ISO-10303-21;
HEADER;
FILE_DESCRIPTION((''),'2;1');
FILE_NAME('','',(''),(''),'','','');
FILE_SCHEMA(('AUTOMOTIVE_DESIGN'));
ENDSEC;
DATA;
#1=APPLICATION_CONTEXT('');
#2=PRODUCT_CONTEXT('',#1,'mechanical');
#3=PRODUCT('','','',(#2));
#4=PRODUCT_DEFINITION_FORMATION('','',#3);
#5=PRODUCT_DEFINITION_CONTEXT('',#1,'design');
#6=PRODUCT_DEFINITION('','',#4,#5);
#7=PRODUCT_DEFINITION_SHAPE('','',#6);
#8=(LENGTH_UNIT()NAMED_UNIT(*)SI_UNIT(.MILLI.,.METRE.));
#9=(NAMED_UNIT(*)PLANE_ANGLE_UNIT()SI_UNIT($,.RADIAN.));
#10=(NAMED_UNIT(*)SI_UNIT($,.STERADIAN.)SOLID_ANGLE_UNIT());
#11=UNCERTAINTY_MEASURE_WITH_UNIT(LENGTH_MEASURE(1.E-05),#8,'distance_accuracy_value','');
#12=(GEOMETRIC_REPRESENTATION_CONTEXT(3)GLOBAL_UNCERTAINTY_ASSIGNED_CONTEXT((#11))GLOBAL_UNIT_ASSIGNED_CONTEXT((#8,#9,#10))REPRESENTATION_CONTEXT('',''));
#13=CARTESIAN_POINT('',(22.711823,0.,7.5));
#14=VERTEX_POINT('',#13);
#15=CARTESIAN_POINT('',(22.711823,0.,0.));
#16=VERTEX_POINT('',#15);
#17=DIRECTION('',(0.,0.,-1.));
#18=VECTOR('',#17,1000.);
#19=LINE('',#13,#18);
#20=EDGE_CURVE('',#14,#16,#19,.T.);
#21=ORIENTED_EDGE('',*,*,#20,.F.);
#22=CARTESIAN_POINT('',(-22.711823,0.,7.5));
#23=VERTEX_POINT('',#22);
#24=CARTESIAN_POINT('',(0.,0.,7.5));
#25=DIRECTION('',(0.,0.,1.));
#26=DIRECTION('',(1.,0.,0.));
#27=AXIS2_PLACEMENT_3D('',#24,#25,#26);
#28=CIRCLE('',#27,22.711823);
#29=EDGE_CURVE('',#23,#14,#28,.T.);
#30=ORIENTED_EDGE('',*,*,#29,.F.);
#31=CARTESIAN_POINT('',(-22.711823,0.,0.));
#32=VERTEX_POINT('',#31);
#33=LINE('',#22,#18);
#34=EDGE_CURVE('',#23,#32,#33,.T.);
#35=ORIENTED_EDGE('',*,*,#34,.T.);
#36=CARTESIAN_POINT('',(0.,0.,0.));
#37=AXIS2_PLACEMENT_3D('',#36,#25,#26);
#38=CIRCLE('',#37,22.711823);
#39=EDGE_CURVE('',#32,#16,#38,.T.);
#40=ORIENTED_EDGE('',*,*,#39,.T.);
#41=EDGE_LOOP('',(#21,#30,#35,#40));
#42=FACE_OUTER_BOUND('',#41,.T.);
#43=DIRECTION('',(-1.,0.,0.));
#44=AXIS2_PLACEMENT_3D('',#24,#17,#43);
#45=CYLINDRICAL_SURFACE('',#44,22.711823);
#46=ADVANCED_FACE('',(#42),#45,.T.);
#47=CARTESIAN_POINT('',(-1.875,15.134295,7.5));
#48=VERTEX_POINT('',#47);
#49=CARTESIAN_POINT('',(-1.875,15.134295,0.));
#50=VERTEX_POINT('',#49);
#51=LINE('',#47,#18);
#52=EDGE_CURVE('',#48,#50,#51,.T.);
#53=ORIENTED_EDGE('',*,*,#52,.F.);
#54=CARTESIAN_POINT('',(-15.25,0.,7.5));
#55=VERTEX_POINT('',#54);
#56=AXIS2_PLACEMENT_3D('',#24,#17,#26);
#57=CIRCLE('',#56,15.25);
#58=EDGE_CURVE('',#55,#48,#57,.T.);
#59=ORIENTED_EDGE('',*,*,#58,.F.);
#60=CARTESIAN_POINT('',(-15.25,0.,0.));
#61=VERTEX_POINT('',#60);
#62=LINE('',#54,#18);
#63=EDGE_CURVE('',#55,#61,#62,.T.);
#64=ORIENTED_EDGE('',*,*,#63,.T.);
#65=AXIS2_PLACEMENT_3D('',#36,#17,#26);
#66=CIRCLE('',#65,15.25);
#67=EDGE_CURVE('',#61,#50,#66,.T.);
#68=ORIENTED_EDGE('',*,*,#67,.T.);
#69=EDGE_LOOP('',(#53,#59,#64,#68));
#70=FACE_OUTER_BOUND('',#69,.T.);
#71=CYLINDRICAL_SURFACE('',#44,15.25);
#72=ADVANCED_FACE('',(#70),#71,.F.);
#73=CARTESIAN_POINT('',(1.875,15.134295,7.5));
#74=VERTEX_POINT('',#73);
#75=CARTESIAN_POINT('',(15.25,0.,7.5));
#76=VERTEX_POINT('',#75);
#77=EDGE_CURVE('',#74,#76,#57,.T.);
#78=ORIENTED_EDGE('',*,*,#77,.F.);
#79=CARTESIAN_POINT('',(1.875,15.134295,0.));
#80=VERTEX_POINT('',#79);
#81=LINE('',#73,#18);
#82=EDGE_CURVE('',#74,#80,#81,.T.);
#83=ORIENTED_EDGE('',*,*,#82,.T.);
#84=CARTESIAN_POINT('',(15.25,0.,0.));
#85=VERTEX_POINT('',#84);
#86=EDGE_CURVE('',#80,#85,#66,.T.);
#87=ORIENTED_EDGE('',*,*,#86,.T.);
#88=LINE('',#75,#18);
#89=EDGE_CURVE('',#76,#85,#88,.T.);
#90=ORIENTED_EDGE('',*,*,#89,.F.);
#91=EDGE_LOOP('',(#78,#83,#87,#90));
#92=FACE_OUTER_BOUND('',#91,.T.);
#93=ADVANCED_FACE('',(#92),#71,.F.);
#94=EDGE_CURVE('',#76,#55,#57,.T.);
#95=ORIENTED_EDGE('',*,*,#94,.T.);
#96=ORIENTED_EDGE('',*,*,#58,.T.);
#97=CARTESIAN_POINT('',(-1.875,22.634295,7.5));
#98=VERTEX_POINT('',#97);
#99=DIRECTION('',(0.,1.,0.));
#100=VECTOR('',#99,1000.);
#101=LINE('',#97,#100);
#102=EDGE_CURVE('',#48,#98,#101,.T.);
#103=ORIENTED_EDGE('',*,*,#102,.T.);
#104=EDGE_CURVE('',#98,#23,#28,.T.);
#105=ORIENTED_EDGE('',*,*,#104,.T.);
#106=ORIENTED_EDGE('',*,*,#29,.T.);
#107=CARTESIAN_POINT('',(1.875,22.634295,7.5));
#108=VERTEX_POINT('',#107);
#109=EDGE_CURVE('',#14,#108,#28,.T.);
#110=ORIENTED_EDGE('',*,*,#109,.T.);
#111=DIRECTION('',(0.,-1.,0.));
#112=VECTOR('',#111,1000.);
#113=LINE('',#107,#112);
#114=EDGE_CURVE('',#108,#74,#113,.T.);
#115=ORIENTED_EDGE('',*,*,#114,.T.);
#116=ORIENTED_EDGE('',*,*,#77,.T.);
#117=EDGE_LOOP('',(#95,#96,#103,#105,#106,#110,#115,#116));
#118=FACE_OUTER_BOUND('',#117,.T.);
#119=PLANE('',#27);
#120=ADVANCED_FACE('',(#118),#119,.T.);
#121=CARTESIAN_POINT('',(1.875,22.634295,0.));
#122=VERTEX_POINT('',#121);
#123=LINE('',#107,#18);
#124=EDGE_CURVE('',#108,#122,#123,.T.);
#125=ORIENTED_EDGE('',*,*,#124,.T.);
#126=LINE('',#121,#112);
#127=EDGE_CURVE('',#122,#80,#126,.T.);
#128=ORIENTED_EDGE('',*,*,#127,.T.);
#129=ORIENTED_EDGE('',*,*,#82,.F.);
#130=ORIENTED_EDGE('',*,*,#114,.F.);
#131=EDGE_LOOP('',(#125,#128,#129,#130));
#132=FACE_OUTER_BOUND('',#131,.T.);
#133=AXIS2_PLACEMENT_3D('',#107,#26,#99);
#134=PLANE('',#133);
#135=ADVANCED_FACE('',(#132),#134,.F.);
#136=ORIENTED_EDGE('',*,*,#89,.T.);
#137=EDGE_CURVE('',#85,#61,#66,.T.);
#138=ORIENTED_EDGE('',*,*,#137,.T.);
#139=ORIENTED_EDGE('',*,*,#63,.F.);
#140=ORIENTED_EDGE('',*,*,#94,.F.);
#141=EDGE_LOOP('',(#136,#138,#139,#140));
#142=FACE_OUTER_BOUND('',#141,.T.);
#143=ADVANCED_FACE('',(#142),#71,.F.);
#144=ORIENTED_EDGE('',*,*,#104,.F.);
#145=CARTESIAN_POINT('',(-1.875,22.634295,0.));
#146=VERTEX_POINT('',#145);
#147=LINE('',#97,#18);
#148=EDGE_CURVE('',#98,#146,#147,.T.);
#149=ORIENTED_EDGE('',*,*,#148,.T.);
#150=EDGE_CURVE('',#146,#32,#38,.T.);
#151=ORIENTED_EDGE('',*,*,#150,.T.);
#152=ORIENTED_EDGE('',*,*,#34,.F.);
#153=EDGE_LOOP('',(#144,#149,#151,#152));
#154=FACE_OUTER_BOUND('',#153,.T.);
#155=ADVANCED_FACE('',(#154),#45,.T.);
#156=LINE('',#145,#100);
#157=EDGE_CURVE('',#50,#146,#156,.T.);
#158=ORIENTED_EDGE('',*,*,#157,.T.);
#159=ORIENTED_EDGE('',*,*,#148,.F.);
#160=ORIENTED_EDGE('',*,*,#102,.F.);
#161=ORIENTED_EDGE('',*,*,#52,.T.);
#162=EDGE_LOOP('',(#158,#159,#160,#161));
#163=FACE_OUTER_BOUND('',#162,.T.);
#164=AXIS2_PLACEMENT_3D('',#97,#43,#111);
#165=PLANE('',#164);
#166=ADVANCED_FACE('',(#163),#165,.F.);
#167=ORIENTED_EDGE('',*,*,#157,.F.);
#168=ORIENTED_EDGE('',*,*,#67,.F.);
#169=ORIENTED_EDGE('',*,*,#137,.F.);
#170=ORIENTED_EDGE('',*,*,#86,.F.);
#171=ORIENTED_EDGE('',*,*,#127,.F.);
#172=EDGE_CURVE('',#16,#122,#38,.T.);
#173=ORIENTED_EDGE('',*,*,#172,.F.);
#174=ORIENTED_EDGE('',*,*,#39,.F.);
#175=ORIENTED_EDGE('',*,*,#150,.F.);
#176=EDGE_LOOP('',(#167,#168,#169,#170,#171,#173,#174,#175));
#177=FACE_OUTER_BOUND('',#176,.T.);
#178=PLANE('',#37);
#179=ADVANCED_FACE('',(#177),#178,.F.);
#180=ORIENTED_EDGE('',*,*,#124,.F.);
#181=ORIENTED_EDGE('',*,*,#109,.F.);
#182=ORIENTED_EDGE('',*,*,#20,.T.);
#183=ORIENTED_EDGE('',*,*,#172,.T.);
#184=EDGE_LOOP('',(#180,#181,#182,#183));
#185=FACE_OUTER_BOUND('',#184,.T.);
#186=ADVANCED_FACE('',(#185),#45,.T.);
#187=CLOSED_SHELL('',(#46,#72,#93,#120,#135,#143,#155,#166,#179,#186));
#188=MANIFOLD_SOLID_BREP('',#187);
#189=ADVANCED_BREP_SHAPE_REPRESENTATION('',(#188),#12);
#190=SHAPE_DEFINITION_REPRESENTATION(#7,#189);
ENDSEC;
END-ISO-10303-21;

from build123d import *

# Parameters (mm, degrees)
EXTRUDE_1_DEPTH = 7.5


with BuildPart() as part:
    # Sketch 266 → 拉伸1 (new body)
    with BuildSketch(Plane.XY):
        with BuildLine():
            Line((-1.875, 22.634294665), (-1.875, 15.134294665))
            ThreePointArc((-1.875, 15.134294665), (0, -15.25), (1.875, 15.134294665))
            Line((1.875, 15.134294665), (1.875, 22.634294665))
            ThreePointArc((1.875, 22.634294665), (0, -22.711823352), (-1.875, 22.634294665))
        make_face()
    extrude(amount=EXTRUDE_1_DEPTH)


solid = part.part
